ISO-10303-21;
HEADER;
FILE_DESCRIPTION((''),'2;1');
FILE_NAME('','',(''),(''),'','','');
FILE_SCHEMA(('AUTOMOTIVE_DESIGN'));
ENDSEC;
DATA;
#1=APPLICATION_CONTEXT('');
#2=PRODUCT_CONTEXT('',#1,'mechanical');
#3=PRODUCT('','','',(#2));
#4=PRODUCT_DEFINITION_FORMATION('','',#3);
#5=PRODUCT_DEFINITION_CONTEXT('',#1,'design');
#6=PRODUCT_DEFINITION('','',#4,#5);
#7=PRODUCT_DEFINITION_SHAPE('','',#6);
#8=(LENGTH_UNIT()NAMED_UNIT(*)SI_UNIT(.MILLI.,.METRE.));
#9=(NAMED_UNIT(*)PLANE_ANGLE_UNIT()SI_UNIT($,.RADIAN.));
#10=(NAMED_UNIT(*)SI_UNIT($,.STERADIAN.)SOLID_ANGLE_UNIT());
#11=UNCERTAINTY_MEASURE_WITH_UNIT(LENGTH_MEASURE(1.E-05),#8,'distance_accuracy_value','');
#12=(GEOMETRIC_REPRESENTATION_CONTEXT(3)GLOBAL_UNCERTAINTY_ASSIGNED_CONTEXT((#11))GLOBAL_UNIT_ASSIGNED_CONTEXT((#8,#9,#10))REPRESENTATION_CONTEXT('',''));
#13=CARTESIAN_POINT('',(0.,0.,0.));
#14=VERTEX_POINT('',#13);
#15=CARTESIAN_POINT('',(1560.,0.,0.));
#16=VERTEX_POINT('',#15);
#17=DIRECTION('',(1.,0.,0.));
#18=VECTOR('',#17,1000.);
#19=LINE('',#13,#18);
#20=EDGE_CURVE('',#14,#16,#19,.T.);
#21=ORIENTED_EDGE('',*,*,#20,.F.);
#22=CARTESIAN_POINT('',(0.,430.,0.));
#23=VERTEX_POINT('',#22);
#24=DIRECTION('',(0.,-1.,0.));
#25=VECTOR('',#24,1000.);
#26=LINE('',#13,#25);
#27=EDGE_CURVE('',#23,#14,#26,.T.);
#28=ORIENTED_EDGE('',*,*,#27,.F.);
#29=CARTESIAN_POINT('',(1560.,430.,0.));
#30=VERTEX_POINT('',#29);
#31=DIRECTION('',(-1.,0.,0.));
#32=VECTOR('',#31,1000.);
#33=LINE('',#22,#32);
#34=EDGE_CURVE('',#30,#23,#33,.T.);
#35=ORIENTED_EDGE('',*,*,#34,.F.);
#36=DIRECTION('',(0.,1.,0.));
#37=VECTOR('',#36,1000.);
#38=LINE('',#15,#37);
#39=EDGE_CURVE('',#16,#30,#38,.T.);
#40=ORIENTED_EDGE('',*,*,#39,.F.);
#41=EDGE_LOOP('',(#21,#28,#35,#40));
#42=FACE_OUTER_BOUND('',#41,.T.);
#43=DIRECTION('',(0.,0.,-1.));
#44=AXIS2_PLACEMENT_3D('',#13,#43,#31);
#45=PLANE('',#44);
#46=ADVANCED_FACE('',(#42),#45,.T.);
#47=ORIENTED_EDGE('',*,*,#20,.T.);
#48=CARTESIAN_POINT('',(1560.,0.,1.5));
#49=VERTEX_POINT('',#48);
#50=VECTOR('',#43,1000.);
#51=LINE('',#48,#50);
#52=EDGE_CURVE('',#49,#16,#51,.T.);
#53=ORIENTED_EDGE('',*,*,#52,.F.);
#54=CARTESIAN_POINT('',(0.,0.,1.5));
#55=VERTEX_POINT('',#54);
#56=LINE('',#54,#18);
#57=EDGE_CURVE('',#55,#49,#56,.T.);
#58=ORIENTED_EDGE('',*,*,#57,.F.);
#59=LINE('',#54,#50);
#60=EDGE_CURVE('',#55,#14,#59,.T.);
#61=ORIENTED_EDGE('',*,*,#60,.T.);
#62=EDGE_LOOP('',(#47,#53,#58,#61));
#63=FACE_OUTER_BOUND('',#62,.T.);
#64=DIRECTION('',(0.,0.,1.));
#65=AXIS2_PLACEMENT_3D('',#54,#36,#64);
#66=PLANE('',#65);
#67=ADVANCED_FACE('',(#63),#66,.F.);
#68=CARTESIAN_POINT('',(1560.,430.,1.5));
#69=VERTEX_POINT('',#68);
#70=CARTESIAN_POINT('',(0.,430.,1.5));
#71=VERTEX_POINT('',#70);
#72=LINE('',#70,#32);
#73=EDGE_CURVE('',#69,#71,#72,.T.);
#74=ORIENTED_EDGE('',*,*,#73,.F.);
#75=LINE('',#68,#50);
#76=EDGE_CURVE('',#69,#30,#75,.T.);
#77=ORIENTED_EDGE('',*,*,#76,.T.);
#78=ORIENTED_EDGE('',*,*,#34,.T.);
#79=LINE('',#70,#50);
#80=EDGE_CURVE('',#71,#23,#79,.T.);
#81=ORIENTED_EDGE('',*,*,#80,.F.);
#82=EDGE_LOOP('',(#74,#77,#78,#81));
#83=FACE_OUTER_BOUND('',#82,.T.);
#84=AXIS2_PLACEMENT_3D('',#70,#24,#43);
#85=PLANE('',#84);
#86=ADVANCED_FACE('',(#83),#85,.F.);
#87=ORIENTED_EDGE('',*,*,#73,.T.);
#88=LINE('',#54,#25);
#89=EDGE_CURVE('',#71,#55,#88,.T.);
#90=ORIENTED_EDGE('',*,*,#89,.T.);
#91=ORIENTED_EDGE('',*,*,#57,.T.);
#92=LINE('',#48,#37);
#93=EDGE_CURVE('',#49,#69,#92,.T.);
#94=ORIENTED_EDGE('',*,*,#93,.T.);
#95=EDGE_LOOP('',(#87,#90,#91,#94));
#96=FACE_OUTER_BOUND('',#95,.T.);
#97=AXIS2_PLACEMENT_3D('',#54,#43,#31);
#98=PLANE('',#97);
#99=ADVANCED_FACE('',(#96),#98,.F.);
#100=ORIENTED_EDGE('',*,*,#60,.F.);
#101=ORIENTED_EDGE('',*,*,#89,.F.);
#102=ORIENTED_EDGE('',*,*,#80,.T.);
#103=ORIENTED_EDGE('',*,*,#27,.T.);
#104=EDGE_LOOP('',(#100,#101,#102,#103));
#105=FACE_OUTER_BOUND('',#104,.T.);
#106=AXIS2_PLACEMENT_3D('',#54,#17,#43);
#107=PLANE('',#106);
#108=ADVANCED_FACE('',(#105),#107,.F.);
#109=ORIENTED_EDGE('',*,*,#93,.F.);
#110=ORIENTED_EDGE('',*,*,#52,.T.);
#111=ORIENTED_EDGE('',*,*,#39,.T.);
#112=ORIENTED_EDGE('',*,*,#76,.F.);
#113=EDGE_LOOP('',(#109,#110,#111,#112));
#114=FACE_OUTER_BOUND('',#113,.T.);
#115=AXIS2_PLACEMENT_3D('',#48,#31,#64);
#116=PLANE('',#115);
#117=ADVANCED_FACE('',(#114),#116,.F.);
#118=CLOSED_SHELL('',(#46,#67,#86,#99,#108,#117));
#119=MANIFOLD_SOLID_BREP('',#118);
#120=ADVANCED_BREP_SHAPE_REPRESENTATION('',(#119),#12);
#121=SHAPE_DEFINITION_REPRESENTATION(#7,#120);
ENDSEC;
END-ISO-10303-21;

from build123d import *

# Parameters (mm, degrees)
SKETCH1_W           = 1560
SKETCH1_H           = 430
BOSS_EXTRUDE1_DEPTH = 1.5


with BuildPart() as part:
    # Sketch1 → Boss-Extrude1 (new body)
    with BuildSketch(Plane.XY):
        with Locations((780, 215)):
            Rectangle(SKETCH1_W, SKETCH1_H)
    extrude(amount=BOSS_EXTRUDE1_DEPTH)


solid = part.part
